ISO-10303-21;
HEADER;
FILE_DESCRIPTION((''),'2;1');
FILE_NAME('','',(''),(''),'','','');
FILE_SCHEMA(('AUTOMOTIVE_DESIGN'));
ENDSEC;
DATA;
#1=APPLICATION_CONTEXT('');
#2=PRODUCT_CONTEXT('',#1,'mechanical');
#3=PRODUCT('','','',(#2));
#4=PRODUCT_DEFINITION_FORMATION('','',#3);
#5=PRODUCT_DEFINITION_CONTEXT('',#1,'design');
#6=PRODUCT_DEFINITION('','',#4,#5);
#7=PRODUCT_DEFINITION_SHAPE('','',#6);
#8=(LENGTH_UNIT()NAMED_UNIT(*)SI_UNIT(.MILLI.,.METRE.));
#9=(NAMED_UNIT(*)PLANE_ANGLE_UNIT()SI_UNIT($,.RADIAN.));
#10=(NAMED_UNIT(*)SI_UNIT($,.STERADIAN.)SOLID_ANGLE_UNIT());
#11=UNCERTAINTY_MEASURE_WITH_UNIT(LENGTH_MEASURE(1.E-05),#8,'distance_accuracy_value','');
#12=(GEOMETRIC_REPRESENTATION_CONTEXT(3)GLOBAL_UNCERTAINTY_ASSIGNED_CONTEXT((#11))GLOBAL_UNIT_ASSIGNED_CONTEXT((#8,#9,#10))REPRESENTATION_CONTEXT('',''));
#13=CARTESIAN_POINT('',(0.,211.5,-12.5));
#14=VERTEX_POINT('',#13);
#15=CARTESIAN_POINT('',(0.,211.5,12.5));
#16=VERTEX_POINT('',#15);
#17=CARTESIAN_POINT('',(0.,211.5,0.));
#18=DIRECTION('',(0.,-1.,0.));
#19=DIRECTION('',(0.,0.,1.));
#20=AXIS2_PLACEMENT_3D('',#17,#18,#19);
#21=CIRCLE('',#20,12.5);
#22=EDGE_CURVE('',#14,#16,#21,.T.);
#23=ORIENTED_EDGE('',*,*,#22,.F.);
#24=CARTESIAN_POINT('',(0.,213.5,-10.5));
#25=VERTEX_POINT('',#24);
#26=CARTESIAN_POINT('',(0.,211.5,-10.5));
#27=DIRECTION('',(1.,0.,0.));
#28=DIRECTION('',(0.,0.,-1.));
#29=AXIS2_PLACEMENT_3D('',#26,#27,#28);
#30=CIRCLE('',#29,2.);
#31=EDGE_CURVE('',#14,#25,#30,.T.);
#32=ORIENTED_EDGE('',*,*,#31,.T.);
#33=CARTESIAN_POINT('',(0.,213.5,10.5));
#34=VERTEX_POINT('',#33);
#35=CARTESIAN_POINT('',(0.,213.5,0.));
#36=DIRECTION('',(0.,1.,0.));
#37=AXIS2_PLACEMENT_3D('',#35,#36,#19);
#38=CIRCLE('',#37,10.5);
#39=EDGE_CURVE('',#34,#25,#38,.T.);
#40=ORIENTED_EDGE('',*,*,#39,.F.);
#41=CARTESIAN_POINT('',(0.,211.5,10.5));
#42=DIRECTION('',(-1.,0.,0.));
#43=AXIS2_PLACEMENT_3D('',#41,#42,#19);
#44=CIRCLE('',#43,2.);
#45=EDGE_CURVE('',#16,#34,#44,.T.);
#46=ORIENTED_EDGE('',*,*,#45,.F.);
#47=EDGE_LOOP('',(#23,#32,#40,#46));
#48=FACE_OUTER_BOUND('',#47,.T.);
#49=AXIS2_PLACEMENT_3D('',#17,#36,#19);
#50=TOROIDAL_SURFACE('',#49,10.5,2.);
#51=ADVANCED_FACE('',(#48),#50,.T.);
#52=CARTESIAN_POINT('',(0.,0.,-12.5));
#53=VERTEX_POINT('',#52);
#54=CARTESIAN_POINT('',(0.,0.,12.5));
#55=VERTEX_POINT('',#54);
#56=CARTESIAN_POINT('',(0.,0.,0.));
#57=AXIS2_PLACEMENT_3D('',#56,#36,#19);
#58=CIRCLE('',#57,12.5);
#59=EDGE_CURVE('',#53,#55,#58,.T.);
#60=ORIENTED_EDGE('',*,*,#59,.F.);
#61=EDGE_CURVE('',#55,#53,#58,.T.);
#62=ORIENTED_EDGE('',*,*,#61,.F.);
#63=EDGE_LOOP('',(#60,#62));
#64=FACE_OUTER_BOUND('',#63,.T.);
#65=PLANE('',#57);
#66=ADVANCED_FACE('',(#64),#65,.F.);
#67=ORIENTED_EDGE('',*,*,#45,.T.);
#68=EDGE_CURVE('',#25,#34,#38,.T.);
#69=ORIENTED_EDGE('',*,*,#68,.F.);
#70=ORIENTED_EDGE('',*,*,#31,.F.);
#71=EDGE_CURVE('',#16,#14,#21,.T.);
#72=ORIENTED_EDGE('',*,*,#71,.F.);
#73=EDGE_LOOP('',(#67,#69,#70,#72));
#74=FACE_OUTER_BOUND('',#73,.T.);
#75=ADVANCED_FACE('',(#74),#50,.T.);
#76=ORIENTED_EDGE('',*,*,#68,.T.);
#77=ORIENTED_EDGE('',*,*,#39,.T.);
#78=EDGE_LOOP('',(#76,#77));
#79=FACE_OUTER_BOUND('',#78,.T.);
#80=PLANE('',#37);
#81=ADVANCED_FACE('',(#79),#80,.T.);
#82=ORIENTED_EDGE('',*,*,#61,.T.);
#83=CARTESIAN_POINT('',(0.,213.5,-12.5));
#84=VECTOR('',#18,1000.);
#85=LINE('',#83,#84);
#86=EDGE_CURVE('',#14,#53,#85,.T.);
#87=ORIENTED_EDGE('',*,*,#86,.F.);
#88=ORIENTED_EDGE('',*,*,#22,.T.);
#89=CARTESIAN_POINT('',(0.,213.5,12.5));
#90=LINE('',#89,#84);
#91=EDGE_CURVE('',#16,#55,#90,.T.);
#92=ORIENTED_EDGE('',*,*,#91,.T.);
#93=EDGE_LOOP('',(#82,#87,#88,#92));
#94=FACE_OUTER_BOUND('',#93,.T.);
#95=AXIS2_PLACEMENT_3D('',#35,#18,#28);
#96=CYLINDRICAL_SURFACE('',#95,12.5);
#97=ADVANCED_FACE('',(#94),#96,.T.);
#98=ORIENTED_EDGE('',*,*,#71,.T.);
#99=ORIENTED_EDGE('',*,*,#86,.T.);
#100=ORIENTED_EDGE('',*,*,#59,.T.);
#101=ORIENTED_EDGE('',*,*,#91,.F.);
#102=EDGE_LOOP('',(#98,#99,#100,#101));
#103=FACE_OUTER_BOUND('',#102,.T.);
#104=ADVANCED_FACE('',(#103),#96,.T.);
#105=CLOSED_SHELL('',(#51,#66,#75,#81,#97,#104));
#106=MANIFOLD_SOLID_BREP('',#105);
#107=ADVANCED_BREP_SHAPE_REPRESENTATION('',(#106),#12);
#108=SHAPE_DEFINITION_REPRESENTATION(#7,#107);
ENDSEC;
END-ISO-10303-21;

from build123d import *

# Parameters (mm, degrees)
SKETCH1_R           = 12.5
BOSS_EXTRUDE1_DEPTH = 213.5
FILLET1_R           = 2


with BuildPart() as part:
    # Sketch1 → Boss-Extrude1 (new body)
    with BuildSketch(Plane(origin=(0, 0, 0), x_dir=(1, 0, 0), z_dir=(0, 1, 0))):
        with Locations(Location((0, 0, 0), (0, 0, 270))):
            Circle(SKETCH1_R)
    extrude(amount=BOSS_EXTRUDE1_DEPTH)

    # Fillet1
    fillet1_edges = [part.edges().sort_by_distance(p)[0] for p in [
        (0, 213.5, -12.5),
    ]]
    fillet(fillet1_edges, radius=FILLET1_R)


solid = part.part
